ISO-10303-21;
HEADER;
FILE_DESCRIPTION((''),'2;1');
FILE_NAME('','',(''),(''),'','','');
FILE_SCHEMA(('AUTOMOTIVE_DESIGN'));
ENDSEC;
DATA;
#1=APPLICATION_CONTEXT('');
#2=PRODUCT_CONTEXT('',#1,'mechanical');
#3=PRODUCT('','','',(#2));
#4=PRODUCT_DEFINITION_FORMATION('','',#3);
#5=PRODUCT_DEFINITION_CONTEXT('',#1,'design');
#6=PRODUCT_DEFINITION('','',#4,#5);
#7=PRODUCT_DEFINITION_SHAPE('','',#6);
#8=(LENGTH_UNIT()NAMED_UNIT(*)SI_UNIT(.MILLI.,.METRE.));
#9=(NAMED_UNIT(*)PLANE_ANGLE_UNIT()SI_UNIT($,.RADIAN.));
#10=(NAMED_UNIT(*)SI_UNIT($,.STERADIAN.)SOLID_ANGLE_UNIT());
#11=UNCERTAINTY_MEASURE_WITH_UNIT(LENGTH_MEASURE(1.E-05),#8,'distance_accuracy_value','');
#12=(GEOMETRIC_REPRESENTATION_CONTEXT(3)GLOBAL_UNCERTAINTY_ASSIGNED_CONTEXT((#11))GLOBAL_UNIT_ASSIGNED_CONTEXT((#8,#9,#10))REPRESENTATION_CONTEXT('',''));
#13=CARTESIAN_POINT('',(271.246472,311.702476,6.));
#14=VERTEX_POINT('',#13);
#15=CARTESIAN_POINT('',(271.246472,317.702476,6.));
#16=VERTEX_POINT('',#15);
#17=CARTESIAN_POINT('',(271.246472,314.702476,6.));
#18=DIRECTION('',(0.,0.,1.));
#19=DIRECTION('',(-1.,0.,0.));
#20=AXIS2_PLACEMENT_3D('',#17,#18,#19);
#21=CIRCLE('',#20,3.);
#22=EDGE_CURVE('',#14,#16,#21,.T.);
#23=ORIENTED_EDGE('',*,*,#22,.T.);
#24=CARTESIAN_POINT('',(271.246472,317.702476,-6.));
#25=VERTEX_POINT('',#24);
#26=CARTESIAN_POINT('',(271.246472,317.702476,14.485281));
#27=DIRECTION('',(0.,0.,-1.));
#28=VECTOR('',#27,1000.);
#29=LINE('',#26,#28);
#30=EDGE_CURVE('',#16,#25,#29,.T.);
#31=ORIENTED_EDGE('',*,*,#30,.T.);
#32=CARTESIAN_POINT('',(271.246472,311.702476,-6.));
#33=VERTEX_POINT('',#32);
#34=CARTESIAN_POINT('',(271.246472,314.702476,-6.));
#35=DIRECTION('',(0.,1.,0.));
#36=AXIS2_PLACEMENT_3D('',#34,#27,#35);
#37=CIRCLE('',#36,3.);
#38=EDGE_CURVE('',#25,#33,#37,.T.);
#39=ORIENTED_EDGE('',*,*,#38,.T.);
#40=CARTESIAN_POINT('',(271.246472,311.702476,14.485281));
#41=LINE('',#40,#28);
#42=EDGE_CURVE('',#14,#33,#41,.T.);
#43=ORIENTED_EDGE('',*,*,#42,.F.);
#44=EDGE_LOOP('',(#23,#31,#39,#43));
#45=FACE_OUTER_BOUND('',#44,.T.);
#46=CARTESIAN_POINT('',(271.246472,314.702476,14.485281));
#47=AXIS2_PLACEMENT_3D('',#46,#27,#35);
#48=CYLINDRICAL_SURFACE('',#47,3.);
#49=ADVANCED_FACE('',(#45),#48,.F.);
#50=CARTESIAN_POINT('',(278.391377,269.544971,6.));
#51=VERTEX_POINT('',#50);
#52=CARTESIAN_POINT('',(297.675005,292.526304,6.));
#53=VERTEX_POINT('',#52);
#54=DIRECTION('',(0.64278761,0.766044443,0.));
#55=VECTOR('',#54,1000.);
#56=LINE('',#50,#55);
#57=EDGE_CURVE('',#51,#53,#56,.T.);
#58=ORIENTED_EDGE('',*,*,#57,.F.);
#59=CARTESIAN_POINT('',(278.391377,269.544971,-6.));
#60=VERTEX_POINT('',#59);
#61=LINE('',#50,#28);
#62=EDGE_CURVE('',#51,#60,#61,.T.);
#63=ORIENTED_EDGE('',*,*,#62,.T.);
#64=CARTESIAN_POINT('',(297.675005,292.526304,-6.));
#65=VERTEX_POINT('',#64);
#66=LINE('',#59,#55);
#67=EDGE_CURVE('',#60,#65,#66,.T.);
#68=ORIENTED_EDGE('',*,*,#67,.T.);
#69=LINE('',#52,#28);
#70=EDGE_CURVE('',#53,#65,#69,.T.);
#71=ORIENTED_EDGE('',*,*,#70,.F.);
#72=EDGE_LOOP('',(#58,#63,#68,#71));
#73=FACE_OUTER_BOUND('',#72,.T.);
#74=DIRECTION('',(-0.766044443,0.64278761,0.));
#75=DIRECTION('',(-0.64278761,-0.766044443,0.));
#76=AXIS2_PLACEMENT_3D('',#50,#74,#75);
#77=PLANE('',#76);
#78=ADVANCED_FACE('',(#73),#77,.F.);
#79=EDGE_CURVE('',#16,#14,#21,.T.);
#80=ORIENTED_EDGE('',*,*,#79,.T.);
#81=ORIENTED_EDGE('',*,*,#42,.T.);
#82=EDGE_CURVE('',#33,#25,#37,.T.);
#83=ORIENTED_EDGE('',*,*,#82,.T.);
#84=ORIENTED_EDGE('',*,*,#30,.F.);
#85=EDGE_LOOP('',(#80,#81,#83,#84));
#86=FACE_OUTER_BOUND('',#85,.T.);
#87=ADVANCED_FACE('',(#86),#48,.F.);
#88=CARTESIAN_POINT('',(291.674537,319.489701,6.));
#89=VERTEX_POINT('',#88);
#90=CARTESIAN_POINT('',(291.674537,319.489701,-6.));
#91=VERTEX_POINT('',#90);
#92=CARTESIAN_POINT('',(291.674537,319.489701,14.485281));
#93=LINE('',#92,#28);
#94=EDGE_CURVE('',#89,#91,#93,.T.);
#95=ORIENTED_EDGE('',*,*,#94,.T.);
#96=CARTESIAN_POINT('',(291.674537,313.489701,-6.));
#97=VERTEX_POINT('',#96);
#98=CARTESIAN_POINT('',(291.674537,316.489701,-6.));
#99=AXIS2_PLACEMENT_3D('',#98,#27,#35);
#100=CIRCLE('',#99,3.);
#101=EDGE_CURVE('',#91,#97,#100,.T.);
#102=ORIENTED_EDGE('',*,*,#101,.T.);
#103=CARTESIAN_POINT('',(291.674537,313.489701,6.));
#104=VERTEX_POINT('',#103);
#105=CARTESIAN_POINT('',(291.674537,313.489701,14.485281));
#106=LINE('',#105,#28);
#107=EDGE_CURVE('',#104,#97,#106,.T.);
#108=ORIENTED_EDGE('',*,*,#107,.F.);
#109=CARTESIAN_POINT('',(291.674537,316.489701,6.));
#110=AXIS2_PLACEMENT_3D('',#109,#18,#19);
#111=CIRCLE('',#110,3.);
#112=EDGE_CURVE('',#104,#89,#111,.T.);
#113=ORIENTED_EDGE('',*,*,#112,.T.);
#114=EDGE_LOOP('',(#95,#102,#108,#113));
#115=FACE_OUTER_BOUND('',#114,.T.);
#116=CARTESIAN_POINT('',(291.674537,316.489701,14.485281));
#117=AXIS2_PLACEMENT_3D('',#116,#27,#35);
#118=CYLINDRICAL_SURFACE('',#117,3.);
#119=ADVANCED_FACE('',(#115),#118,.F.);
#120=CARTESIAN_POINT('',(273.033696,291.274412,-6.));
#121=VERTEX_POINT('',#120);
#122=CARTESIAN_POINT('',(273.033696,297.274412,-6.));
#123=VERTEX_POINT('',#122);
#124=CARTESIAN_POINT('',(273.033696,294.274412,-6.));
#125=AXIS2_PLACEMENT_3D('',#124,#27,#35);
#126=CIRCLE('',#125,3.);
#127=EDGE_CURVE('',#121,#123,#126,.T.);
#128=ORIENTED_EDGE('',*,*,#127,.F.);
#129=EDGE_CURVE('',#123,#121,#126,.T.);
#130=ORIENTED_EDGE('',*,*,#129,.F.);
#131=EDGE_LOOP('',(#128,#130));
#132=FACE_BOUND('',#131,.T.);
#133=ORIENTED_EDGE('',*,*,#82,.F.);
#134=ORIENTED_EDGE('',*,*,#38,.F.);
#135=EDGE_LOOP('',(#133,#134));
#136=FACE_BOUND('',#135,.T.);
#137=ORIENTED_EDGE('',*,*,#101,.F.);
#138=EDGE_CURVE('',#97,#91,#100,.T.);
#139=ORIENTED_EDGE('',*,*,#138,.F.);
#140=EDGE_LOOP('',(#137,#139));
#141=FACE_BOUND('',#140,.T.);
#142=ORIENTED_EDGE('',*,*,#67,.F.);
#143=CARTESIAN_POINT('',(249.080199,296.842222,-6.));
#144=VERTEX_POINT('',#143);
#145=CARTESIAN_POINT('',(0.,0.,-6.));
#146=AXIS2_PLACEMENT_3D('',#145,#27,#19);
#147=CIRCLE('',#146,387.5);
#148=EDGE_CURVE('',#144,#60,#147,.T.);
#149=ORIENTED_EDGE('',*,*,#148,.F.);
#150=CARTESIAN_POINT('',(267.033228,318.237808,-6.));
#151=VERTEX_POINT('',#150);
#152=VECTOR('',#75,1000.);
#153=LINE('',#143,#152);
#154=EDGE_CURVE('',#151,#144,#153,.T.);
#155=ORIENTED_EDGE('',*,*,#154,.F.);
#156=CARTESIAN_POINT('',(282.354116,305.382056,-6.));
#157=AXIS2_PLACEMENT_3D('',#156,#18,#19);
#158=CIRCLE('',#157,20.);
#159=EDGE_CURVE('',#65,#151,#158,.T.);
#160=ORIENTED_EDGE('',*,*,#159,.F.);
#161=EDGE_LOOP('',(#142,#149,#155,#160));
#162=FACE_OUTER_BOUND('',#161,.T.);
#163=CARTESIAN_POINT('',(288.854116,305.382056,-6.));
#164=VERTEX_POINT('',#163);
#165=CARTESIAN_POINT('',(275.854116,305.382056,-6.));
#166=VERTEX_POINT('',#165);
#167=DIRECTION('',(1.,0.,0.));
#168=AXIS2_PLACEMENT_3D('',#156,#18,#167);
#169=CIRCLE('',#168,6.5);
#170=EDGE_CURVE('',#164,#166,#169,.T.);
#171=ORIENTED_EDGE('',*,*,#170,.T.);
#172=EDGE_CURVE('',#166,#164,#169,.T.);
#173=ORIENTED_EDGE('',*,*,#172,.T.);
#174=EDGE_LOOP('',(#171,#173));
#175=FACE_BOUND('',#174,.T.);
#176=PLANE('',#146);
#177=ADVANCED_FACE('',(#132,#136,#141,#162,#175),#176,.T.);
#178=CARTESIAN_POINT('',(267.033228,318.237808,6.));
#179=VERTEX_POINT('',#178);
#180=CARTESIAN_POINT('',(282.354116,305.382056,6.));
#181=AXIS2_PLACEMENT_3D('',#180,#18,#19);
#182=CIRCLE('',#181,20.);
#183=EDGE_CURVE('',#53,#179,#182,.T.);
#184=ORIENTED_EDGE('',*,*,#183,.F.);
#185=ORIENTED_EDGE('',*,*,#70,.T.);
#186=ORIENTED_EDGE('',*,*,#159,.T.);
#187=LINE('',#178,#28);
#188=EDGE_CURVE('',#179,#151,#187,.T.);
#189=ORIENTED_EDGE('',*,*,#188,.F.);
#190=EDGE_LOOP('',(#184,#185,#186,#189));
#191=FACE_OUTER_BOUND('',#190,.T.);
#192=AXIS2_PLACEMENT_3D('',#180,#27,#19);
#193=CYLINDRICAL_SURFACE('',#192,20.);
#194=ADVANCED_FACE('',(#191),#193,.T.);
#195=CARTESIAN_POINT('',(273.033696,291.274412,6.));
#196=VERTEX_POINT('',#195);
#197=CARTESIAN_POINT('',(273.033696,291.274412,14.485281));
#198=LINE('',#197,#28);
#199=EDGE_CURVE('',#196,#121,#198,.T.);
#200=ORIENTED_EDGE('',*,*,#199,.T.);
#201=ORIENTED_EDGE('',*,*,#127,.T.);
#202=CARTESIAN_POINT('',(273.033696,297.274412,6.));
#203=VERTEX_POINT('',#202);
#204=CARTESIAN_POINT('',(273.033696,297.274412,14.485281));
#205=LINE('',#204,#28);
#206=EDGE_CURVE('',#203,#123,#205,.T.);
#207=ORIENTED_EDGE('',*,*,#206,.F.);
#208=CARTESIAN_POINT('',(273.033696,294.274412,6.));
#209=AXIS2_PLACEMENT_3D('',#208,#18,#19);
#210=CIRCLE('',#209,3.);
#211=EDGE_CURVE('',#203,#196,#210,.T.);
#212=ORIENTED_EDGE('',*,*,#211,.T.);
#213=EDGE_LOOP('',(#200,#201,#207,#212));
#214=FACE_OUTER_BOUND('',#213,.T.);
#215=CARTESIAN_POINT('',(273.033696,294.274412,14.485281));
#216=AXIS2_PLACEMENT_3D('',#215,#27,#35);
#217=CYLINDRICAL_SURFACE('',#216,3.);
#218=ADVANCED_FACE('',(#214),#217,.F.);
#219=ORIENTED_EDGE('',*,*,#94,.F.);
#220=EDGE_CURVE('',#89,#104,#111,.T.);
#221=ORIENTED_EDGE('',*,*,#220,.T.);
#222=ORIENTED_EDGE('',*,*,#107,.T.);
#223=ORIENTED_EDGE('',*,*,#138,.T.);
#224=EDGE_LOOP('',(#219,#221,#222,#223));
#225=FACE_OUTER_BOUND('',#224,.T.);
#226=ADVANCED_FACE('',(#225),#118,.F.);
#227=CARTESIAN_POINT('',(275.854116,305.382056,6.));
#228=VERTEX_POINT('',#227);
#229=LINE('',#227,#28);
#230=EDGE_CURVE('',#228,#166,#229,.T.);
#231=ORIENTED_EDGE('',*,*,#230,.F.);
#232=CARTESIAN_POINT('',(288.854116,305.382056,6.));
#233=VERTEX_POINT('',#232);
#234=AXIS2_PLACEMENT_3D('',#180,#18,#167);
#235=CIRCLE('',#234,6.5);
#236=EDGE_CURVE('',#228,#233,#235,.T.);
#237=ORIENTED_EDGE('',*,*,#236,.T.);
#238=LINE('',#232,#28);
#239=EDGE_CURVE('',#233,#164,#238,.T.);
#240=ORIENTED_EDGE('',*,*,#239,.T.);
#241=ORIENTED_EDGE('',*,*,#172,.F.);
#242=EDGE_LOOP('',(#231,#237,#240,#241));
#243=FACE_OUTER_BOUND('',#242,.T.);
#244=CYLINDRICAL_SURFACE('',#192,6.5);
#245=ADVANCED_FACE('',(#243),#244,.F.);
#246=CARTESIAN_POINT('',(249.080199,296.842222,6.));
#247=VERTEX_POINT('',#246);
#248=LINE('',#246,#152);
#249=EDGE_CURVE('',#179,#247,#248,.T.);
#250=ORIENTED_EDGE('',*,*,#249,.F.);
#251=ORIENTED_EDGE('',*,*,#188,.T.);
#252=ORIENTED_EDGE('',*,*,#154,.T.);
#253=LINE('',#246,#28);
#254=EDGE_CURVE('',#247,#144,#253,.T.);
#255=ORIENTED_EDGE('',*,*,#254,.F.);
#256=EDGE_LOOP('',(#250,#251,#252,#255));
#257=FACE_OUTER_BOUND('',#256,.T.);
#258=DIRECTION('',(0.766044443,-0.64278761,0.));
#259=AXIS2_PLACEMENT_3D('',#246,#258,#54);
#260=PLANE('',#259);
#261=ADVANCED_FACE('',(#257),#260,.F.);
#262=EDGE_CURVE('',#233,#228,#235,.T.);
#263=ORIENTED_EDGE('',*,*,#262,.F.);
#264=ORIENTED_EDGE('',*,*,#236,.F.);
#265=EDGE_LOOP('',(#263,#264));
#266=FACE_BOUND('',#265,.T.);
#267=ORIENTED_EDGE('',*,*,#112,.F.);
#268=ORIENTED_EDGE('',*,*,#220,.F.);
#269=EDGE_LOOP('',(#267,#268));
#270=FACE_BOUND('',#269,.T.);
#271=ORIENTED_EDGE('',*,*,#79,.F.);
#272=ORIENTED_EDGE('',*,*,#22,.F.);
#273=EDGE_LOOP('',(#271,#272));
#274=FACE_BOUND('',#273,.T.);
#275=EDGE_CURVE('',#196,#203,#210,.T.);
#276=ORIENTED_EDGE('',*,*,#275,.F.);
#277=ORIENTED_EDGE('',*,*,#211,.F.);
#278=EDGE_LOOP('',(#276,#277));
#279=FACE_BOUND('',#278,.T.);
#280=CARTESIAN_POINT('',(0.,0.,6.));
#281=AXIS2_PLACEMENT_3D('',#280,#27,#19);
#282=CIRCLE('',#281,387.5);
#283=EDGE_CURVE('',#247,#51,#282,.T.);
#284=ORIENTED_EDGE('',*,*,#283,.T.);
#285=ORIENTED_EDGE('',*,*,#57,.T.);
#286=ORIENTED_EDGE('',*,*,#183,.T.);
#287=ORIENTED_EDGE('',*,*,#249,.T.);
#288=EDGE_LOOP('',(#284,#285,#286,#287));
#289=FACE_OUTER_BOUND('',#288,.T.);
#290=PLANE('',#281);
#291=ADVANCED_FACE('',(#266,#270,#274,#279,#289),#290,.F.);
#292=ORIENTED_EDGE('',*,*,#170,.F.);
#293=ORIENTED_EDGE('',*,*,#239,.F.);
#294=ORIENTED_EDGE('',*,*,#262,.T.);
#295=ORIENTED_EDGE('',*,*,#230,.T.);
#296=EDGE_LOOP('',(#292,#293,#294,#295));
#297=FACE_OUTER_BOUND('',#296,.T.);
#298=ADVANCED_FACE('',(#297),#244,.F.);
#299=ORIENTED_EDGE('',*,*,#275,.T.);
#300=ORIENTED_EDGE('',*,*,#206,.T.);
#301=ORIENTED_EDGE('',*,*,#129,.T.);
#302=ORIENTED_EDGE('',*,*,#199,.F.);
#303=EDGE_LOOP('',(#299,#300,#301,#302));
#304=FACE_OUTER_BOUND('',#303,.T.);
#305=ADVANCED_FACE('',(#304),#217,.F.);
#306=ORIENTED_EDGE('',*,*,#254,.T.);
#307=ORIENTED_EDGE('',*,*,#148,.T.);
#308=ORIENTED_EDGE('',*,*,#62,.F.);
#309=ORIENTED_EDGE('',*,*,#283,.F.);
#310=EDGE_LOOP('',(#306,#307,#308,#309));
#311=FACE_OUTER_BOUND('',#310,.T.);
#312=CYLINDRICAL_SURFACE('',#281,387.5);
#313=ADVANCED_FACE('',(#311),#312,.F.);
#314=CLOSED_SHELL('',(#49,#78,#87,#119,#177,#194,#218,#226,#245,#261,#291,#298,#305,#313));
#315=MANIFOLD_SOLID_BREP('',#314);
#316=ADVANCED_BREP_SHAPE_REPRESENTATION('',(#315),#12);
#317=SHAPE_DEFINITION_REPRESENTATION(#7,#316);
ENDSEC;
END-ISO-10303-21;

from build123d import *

# Parameters (mm, degrees)
SKETCH1_R           = 6.499999992
BOSS_EXTRUDE1_DEPTH = 6
SKETCH2_R           = 3
CUT_EXTRUDE1_DEPTH  = 12


with BuildPart() as part:
    # Sketch1 → Boss-Extrude1 (new, symmetric)
    with BuildSketch(Plane.XY):
        with BuildLine():
            Line((249.080198754, 296.842221709), (267.033227589, 318.237808321))
            ThreePointArc((267.033227589, 318.237808321), (295.209868645, 320.702944991), (297.675005315, 292.526303935))
            Line((297.675005315, 292.526303935), (278.391377025, 269.544970642))
            ThreePointArc((278.391377025, 269.544970642), (264.088717655, 283.572564272), (249.080198754, 296.842221709))
        make_face()
        with Locations((282.354116452, 305.382056128)):
            Circle(SKETCH1_R, mode=Mode.SUBTRACT)
    extrude(amount=BOSS_EXTRUDE1_DEPTH, both=True)

    # Sketch2 → Cut-Extrude1 (cut)
    with BuildSketch(Plane(origin=(0, 0, -6), x_dir=(-1, 0, 0), z_dir=(0, 0, -1))):
        with Locations(Location((-291.674536792, 316.489700554, 0), (0, 0, 90))):
            Circle(SKETCH2_R)
        with Locations(Location((-271.246472026, 314.702476468, 0), (0, 0, 90))):
            Circle(SKETCH2_R)
        with Locations(Location((-273.033696112, 294.274411702, 0), (0, 0, 90))):
            Circle(SKETCH2_R)
    extrude(amount=-CUT_EXTRUDE1_DEPTH, mode=Mode.SUBTRACT)


solid = part.part
